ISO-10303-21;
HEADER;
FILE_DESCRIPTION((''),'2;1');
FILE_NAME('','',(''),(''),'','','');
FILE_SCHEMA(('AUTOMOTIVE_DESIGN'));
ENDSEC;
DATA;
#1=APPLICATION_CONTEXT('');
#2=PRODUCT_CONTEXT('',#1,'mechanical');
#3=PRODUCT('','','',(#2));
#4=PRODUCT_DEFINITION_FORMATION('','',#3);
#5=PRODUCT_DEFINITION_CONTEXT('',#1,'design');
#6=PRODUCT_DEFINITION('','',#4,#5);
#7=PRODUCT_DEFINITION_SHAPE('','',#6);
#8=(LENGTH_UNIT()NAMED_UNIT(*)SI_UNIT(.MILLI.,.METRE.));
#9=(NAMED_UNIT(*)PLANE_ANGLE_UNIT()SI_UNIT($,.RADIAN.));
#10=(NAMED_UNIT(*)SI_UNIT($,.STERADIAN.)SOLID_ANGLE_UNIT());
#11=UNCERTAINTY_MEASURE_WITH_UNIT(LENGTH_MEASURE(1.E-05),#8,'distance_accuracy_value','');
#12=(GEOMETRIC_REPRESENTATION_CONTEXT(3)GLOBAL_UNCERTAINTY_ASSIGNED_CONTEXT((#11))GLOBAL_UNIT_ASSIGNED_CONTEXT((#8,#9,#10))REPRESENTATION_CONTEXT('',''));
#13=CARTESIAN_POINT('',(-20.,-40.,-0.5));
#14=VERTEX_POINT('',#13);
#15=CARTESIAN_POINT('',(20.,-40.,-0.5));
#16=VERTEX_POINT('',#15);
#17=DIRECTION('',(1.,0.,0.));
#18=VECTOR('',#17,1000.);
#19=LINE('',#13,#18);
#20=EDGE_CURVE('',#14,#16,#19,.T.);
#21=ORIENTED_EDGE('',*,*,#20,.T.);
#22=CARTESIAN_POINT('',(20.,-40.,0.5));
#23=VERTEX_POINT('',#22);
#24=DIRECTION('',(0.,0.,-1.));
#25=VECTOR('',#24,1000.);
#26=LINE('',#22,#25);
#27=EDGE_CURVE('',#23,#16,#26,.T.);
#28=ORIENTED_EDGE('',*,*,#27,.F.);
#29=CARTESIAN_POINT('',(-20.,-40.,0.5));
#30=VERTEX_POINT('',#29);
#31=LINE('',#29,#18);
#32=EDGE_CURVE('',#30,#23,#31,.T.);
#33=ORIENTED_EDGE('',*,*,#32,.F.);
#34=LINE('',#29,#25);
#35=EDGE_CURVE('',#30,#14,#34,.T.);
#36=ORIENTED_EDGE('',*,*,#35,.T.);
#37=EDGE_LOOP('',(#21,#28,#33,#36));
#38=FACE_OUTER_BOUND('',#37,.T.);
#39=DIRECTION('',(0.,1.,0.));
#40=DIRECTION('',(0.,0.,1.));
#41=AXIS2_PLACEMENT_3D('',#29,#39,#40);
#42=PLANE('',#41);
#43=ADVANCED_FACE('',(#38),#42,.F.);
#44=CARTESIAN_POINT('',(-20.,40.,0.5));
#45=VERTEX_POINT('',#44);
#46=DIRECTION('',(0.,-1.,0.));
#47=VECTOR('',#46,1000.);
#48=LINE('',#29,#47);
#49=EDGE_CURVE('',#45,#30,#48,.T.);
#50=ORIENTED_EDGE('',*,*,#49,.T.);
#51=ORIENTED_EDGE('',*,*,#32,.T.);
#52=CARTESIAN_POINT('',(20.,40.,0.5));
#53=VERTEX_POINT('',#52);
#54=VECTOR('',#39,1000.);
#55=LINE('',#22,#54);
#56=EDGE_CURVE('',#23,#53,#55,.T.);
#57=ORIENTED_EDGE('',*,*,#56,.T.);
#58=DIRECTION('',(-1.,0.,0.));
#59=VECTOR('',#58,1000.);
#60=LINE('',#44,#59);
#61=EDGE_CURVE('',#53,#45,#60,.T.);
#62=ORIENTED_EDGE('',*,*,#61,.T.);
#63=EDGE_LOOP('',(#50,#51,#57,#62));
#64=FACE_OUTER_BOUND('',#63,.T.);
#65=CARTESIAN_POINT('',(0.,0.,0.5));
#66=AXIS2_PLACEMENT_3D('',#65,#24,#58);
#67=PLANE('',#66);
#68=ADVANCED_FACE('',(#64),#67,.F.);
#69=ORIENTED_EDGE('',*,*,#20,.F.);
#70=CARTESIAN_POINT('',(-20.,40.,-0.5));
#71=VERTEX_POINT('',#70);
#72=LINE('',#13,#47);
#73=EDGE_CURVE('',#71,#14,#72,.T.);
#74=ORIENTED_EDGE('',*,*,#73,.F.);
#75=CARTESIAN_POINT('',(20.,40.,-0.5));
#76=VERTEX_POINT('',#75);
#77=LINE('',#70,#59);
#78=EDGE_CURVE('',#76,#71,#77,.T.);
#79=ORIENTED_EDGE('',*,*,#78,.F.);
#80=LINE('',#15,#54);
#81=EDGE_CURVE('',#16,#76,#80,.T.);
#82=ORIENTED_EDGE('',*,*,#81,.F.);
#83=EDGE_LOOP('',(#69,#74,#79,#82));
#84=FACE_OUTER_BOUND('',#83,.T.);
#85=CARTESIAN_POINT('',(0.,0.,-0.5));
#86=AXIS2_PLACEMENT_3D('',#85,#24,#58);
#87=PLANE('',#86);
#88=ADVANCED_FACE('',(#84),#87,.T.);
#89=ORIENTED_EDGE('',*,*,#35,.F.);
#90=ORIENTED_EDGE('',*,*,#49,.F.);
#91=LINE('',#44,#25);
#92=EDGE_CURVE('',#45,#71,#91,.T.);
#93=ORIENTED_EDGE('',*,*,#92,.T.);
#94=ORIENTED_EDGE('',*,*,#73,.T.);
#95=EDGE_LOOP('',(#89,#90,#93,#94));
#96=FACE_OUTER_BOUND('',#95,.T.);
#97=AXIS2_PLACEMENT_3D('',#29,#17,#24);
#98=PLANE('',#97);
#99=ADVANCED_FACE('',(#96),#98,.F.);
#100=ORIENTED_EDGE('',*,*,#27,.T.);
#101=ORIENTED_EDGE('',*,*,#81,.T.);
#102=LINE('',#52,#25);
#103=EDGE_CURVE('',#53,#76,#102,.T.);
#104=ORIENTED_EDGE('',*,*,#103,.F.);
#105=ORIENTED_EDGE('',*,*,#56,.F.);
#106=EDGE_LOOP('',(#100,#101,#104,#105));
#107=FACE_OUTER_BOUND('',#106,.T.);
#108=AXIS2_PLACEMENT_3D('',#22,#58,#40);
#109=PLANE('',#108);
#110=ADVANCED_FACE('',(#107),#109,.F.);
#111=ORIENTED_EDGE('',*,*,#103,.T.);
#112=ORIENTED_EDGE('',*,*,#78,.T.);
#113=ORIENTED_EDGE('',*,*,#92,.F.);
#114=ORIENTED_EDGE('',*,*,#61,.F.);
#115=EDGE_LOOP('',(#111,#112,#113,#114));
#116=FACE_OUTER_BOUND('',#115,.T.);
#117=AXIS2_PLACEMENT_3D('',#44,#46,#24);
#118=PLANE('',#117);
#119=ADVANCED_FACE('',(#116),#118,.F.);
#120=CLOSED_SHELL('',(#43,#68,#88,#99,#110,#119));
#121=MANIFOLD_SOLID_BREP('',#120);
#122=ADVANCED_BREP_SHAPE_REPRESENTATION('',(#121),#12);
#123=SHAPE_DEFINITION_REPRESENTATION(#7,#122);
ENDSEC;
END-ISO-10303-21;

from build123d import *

# Parameters (mm, degrees)
SKETCH_1_W      = 40
SKETCH_1_H      = 80
EXTRUDE_1_DEPTH = 0.5


with BuildPart() as part:
    # 草图1 → 凸台-拉伸1 (new, symmetric)
    with BuildSketch(Plane.XY):
        Rectangle(SKETCH_1_W, SKETCH_1_H)
    extrude(amount=EXTRUDE_1_DEPTH, both=True)


solid = part.part
